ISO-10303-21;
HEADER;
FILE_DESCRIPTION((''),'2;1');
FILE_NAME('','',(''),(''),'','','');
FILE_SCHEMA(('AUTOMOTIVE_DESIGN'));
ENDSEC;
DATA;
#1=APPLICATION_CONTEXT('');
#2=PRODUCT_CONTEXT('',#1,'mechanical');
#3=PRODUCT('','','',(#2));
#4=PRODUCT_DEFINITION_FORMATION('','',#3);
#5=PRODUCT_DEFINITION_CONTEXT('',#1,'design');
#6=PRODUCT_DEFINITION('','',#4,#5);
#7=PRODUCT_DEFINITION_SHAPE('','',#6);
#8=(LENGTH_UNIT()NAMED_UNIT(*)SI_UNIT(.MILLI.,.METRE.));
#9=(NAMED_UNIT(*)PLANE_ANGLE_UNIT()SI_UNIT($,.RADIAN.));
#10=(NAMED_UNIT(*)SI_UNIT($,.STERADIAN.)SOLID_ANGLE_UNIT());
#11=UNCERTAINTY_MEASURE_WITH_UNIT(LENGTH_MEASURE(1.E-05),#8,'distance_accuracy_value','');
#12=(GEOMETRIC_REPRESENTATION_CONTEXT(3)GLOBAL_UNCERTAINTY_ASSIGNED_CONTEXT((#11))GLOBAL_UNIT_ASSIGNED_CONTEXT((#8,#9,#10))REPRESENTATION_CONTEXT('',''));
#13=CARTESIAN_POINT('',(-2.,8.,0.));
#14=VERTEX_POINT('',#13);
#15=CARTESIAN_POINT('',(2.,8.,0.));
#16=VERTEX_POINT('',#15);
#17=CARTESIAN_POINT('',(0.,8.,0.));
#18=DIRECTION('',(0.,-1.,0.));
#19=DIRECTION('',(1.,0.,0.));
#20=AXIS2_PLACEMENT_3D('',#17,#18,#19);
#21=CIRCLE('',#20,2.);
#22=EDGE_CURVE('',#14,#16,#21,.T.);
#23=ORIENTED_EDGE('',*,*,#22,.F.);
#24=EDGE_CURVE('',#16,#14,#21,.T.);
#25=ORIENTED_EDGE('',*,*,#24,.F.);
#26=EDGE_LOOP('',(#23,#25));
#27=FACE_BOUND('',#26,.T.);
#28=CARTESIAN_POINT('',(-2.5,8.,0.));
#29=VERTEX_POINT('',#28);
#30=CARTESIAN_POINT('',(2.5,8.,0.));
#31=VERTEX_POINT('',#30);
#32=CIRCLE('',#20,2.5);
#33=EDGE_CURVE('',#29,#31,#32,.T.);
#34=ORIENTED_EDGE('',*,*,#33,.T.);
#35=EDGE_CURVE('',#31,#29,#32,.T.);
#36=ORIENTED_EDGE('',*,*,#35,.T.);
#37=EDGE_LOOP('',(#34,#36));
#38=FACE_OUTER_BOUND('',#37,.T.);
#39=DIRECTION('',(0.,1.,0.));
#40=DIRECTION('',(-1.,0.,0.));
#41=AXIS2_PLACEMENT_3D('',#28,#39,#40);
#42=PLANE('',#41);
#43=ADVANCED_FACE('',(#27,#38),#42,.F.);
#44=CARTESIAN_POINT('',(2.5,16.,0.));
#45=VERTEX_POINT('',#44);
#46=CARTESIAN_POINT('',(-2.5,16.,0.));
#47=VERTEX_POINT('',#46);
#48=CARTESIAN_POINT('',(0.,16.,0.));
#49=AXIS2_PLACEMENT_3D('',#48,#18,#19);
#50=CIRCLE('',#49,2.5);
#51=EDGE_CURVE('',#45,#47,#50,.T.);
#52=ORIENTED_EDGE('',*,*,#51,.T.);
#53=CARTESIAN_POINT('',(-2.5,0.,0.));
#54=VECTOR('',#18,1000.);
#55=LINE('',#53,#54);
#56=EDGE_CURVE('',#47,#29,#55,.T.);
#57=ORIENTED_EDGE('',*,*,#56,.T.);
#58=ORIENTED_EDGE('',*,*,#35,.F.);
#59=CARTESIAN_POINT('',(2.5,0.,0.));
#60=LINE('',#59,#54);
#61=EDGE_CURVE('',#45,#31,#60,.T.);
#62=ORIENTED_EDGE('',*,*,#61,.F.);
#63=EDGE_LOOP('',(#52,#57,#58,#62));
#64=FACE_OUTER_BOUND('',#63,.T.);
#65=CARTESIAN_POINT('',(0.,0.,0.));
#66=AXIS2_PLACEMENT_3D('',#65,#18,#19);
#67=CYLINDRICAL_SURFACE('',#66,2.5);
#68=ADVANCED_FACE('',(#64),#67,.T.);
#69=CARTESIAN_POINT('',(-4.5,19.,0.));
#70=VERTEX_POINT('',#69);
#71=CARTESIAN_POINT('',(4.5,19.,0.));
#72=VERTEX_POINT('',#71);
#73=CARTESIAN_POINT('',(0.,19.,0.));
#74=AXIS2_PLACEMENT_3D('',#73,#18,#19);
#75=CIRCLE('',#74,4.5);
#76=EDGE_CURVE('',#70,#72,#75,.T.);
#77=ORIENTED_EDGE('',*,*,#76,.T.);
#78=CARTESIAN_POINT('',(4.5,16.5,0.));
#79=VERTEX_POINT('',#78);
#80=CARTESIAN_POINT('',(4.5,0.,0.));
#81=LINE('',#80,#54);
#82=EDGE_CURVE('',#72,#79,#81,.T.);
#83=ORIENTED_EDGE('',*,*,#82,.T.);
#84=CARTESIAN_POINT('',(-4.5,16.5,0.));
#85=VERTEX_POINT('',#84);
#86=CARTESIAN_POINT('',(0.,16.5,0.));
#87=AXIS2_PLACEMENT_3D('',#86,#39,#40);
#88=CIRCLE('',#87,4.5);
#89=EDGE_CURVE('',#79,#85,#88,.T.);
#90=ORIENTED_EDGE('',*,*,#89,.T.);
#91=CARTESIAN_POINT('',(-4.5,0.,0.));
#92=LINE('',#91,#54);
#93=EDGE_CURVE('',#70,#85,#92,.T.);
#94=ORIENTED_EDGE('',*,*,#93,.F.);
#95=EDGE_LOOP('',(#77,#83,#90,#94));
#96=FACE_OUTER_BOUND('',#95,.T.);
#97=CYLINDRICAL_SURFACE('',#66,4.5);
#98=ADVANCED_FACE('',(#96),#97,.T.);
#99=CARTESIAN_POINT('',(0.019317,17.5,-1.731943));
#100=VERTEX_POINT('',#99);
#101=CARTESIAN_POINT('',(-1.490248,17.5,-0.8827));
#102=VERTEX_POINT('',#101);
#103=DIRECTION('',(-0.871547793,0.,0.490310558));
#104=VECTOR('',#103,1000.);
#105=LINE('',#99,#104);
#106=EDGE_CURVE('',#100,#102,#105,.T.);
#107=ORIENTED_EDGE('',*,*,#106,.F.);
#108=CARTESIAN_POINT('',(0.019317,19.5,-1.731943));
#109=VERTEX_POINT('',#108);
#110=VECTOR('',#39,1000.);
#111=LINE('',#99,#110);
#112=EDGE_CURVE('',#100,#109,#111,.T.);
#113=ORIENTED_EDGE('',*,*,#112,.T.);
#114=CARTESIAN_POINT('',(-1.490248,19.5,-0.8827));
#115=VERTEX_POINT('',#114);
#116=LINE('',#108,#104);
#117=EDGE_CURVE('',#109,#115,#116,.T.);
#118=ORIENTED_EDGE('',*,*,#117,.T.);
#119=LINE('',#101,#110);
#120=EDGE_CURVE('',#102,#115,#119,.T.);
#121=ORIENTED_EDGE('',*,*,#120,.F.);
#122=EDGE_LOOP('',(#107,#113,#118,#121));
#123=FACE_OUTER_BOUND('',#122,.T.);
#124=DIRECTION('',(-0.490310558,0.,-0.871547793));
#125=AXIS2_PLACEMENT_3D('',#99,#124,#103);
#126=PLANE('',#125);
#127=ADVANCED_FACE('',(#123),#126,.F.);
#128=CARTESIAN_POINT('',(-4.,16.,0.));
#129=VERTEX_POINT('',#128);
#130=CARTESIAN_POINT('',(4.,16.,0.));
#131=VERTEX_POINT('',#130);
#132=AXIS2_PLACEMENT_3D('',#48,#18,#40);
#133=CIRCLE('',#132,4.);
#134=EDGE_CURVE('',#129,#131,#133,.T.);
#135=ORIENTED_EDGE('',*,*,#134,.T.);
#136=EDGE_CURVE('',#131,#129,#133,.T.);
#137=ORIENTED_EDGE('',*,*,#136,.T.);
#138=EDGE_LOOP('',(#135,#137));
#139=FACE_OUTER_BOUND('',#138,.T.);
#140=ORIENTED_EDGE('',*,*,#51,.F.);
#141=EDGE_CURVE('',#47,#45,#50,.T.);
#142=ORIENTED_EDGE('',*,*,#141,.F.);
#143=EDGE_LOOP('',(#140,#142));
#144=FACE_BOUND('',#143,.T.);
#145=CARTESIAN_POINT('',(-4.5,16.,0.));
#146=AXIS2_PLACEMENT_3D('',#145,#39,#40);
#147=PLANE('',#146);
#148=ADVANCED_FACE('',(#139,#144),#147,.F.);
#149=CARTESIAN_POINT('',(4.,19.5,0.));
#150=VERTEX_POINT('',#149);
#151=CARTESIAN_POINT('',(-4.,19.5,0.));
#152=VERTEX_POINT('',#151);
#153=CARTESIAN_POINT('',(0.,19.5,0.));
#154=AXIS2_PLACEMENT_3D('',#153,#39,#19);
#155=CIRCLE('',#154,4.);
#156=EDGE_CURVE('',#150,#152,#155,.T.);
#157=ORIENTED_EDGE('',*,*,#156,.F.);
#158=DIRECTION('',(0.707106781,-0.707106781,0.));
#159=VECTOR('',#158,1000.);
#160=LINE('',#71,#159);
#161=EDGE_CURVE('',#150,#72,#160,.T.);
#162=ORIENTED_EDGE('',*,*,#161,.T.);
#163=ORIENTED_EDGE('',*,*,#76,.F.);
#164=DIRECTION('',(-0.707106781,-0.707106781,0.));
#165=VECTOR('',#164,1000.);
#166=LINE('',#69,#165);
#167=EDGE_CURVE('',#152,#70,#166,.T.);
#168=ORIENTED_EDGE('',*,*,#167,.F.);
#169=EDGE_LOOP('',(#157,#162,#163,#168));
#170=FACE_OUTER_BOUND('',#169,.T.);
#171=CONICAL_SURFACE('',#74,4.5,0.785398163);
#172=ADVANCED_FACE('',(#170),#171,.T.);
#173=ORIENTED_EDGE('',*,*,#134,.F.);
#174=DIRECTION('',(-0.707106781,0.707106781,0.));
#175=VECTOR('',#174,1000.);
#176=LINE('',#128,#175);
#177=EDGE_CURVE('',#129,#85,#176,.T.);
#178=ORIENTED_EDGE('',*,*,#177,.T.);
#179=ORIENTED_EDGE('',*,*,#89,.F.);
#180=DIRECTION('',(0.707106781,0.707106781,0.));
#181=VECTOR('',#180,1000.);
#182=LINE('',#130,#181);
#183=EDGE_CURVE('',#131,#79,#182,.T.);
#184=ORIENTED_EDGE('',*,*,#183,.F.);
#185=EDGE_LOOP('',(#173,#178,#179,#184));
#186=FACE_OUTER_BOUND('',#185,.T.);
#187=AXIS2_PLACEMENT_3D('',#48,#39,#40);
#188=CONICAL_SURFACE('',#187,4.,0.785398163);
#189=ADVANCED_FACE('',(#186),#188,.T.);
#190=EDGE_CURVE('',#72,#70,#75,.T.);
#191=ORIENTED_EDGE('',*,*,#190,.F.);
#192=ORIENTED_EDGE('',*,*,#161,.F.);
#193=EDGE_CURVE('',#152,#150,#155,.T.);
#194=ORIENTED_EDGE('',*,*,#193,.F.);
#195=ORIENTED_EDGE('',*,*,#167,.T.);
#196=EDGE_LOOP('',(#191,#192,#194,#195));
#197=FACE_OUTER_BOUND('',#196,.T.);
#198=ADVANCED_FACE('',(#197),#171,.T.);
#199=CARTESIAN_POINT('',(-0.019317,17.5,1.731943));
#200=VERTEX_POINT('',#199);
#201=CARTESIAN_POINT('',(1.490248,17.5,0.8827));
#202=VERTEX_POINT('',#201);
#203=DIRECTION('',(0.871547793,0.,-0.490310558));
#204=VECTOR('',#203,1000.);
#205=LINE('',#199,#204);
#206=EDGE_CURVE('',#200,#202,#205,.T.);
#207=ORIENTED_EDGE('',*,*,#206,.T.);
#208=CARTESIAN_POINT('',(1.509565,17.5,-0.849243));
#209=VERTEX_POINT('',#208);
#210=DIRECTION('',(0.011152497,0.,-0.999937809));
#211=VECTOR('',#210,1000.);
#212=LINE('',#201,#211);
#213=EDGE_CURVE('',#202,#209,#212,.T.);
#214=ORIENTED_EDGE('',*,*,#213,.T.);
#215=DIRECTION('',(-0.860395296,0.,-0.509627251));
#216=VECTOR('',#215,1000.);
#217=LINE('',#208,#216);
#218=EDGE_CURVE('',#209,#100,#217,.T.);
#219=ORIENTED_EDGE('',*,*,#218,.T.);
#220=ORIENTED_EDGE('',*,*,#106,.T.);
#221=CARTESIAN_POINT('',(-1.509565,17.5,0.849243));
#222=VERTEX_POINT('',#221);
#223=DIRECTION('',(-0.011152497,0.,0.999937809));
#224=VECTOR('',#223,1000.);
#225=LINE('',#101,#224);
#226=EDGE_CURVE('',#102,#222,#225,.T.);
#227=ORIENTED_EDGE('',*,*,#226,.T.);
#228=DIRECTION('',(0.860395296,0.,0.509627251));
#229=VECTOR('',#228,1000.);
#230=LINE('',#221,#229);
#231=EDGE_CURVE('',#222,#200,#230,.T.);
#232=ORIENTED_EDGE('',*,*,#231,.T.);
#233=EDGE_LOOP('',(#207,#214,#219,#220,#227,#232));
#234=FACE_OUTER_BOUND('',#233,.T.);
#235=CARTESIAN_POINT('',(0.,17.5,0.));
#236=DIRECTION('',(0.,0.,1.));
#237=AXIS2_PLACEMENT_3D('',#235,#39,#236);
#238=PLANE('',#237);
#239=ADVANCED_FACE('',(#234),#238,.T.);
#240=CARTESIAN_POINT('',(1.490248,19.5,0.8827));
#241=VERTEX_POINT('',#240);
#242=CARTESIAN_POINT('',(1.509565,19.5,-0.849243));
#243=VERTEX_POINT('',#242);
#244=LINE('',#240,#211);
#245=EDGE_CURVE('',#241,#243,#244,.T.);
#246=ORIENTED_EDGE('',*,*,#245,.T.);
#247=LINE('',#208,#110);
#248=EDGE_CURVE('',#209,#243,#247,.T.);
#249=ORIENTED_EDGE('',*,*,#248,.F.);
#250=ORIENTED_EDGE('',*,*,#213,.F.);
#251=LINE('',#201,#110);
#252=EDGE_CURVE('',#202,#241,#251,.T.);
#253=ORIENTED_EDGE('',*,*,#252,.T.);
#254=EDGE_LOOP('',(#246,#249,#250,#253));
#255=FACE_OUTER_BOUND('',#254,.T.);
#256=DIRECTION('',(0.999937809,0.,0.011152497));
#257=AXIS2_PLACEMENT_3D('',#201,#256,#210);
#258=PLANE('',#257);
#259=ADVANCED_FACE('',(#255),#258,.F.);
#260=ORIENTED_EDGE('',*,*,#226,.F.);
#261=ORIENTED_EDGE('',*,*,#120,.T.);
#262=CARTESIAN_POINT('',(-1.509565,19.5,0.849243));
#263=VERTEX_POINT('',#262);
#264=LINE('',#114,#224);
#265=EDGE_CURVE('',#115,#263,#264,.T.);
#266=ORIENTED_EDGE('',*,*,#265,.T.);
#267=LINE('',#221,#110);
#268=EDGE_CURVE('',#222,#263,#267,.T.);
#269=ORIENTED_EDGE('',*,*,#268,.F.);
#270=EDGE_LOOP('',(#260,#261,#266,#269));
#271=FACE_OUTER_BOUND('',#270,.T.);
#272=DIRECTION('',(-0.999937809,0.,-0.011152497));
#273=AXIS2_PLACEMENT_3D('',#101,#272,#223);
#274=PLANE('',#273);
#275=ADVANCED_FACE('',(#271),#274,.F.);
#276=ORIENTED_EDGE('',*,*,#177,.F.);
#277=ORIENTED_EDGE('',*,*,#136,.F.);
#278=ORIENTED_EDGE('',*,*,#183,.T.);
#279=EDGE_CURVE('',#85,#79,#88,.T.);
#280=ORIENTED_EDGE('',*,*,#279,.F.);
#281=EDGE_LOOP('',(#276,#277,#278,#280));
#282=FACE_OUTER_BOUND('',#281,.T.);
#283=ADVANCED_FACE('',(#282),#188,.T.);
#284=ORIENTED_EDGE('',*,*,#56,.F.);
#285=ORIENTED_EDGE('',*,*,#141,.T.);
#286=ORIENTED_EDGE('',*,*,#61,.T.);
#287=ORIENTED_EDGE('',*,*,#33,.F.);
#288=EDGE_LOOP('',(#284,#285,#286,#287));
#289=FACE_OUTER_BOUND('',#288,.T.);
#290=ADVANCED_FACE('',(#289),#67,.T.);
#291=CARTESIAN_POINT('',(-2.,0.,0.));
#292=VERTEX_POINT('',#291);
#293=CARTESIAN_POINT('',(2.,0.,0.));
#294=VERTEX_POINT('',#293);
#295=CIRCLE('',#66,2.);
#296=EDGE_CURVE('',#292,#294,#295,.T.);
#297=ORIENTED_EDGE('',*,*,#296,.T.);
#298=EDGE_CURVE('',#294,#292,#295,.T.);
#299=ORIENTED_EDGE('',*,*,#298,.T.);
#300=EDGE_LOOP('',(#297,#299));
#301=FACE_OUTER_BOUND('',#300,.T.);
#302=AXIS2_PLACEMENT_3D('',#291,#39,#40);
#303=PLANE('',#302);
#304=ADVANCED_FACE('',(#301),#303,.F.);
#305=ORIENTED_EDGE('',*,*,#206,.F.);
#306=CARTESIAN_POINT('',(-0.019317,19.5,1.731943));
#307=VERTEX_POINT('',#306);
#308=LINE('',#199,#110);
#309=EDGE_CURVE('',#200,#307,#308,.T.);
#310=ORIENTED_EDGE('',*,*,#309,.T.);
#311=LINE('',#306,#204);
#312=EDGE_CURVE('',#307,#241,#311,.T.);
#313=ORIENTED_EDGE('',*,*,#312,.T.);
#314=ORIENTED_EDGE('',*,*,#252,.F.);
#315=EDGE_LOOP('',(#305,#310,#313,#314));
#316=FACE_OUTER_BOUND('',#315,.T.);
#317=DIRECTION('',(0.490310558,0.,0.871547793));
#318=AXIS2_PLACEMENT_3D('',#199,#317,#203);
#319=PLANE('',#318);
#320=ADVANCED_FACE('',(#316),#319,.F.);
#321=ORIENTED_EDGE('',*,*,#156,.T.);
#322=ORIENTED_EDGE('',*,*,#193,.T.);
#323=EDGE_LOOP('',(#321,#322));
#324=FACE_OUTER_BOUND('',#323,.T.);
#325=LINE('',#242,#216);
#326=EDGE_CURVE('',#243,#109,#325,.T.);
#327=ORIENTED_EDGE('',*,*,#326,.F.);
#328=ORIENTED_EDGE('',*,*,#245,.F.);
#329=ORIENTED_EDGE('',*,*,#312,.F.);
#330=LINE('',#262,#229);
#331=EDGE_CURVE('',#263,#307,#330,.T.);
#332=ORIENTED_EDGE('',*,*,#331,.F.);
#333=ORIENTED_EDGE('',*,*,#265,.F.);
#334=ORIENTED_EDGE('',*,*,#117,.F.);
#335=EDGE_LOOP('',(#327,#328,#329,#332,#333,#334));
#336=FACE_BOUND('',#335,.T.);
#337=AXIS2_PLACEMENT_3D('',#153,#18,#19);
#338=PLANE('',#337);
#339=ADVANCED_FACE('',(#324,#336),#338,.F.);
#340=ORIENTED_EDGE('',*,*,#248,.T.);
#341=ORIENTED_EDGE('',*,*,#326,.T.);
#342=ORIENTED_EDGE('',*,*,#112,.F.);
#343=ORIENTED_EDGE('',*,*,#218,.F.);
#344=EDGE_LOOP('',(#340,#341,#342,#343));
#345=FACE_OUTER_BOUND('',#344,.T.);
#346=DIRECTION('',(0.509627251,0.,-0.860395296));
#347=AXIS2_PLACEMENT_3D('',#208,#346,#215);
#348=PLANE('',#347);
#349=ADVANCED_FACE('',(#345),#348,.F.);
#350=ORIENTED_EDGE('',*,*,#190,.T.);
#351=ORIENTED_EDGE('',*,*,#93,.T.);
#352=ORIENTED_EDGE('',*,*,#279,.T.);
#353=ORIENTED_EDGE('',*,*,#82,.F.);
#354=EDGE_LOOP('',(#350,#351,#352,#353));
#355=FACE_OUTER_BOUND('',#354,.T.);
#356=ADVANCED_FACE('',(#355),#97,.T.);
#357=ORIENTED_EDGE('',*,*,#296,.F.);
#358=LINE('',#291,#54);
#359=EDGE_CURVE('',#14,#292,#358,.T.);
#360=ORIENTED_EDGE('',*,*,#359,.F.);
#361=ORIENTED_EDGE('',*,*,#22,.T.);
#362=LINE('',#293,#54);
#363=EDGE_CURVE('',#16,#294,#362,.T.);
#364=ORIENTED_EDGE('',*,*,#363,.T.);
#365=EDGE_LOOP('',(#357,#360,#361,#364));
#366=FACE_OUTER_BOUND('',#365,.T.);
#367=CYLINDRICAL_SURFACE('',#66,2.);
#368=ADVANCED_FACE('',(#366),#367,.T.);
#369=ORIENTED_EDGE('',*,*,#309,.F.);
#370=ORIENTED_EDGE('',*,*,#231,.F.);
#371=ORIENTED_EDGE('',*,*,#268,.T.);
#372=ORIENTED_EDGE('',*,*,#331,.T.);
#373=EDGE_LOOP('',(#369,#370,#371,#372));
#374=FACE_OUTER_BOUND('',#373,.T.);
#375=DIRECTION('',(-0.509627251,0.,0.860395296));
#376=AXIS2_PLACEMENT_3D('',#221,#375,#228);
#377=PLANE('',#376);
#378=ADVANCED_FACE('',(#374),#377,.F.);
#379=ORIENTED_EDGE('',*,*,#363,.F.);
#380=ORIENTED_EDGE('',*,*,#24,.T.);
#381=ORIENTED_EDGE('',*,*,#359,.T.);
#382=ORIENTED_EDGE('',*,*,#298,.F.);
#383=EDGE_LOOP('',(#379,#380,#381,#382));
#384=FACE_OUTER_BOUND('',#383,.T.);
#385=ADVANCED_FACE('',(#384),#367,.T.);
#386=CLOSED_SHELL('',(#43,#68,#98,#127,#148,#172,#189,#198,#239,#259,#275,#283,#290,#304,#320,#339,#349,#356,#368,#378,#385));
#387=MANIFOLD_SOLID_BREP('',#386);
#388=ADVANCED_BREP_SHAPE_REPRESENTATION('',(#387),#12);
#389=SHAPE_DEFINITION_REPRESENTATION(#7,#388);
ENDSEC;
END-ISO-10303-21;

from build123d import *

# Parameters (mm, degrees)
CUT_EXTRUDE1_DEPTH = 2
CHAMFER1_SIZE      = 0.5


with BuildPart() as part:
    # Sketch1 → Revolve1 (revolve)
    with BuildSketch(Plane.XY, mode=Mode.PRIVATE) as revolve1_sk:
        Polygon((0, 0), (0, 19.5), (-4.5, 19.5), (-4.5, 16), (-2.5, 16), (-2.5, 8), (-2, 8), (-2, 0), align=None)
    revolve(revolve1_sk.sketch.rotate(Axis((0, 0, 0), (0, 1, 0)), 180), axis=Axis((0, 0, 0), (0, 1, 0)))

    # Sketch2 → Cut-Extrude1 (cut)
    with BuildSketch(Plane(origin=(0, 19.5, 0), x_dir=(1, 0, 0), z_dir=(0, 1, 0))):
        Polygon((1.50956506, 0.849242799), (0.019316692, 1.73194309), (-1.490248367, 0.882700291), (-1.50956506, -0.849242799), (-0.019316692, -1.73194309), (1.490248367, -0.882700291), align=None)
    extrude(amount=-CUT_EXTRUDE1_DEPTH, mode=Mode.SUBTRACT)

    # Chamfer1
    chamfer1_edges = [part.edges().sort_by_distance(p)[0] for p in [
        (-4.5, 16, 0),
        (-4.5, 19.5, 0),
    ]]
    chamfer(chamfer1_edges, length=CHAMFER1_SIZE)


solid = part.part
